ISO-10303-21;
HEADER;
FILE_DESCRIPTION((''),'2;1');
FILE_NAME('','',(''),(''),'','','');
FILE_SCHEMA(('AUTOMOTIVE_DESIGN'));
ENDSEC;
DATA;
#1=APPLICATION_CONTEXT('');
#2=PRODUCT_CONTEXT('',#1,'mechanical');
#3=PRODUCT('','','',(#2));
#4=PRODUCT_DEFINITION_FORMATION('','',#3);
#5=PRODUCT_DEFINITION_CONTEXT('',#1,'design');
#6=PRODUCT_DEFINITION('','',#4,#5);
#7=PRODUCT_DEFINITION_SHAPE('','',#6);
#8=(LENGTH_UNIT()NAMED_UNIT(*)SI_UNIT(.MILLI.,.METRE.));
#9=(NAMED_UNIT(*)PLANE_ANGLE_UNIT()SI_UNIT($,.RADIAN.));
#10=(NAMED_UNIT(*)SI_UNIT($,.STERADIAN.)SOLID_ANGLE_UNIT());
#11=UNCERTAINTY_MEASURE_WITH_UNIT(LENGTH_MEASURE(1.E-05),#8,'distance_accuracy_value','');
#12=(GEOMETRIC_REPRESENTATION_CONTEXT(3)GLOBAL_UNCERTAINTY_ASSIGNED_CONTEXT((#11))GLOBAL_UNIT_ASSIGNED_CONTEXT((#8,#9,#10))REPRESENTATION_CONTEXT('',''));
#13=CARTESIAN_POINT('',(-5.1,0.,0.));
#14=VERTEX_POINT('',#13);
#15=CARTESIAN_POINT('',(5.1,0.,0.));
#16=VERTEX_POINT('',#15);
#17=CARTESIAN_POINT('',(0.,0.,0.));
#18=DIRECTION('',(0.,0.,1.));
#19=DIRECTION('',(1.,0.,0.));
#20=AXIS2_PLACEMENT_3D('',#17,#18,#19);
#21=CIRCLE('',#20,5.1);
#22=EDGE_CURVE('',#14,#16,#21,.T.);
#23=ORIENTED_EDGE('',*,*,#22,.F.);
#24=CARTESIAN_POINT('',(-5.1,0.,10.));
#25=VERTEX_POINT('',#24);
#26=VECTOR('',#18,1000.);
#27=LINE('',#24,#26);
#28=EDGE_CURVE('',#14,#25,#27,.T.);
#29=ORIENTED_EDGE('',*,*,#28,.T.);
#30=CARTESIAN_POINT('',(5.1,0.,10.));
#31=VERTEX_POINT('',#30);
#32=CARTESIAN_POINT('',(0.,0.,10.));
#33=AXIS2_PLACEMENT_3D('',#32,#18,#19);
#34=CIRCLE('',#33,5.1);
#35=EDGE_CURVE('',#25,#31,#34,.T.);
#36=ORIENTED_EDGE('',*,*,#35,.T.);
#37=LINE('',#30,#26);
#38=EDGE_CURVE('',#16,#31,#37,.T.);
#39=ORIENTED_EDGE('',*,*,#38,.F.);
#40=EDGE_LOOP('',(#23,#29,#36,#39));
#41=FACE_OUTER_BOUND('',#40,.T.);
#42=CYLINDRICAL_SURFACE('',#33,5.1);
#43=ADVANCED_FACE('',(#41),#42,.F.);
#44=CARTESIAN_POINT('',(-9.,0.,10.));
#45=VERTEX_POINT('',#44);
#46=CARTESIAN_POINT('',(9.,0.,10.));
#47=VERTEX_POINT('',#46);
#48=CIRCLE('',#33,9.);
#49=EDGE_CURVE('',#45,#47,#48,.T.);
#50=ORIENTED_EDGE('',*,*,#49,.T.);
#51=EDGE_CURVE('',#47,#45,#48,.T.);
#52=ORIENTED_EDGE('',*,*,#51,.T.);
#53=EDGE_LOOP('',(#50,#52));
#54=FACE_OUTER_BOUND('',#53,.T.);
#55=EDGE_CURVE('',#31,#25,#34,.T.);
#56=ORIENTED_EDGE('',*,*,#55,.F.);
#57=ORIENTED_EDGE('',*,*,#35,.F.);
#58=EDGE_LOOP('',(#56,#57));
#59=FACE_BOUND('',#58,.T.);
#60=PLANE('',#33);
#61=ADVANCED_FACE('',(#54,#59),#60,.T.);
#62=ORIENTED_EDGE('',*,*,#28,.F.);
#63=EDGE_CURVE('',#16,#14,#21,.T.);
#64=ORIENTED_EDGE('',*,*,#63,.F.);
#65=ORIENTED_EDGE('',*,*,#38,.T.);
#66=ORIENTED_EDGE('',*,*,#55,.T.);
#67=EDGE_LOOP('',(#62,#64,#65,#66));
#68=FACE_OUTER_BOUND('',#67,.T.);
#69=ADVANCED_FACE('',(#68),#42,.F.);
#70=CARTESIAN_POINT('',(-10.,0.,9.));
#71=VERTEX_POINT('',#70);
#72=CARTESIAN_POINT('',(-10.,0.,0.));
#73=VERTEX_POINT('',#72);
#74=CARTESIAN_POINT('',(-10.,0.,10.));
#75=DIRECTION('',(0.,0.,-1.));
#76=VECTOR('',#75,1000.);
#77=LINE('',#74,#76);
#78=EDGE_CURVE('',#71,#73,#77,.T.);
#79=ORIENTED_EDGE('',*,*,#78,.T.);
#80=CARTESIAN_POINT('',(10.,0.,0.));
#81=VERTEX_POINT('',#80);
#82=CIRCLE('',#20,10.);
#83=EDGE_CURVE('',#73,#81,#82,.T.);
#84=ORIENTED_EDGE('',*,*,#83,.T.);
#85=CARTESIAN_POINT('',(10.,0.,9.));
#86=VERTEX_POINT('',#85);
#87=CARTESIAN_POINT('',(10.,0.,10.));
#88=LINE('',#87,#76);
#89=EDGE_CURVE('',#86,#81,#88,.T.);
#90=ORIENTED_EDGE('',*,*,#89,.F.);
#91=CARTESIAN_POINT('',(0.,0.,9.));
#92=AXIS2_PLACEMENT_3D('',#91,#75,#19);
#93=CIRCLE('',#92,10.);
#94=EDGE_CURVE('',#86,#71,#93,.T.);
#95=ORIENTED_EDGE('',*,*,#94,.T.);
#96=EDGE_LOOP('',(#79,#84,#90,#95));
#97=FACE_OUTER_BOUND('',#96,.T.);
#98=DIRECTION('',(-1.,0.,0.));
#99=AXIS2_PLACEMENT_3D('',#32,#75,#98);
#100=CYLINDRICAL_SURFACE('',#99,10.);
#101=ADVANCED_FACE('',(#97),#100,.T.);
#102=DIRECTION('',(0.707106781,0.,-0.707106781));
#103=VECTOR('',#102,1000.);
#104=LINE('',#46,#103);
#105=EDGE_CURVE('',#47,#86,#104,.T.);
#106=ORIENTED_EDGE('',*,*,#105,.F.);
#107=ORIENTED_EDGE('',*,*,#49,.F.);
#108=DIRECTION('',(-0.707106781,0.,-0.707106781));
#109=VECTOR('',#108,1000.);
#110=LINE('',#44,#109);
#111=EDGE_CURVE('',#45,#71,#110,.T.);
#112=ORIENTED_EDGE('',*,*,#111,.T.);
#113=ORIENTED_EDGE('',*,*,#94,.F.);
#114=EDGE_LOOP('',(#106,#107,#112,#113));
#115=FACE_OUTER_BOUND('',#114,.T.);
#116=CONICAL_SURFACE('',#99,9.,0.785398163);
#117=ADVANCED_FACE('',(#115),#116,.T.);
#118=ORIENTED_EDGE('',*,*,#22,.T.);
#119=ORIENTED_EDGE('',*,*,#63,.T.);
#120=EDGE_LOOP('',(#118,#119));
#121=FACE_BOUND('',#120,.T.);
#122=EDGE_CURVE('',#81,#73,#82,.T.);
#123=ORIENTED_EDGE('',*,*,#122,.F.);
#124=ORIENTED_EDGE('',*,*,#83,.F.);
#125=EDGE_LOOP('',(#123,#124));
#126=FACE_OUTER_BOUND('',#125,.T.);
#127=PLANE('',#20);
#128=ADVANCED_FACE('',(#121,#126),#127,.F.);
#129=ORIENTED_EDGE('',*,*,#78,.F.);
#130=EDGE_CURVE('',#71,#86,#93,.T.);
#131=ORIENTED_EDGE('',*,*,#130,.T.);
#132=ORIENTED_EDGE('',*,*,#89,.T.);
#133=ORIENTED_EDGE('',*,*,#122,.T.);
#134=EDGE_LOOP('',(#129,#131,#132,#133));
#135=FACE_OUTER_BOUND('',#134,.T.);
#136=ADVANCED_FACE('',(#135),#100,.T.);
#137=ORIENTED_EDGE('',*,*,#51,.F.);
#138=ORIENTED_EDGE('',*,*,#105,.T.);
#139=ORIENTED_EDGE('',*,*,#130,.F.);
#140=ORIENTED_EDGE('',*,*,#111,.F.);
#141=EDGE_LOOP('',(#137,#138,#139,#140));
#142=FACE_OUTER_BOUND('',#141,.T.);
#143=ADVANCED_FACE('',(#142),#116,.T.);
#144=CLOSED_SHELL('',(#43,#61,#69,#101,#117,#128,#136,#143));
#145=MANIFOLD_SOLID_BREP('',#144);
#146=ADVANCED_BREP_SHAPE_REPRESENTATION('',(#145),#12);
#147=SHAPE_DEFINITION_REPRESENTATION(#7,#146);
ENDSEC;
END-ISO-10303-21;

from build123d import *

# Parameters (mm, degrees)
SKETCH_1_R              = 10
EXTRUDE_1_DEPTH         = 10
HOLE_WIZARD_M12_1_D     = 10.2
HOLE_WIZARD_M12_1_DEPTH = 30.25
HOLE_WIZARD_M12_1_TIP   = 3.064389157
CHAMFER_1_SIZE          = 1


with BuildPart() as part:
    # 草图1 → 凸台-拉伸1 (new body)
    with BuildSketch(Plane.XY):
        Circle(SKETCH_1_R)
    extrude(amount=EXTRUDE_1_DEPTH)

    # M12 螺纹孔1
    with Locations(Plane.XY.offset(10)):
        with Locations((0, 0)):
            Hole(HOLE_WIZARD_M12_1_D / 2, depth=HOLE_WIZARD_M12_1_DEPTH)
            with Locations((0, 0, -(HOLE_WIZARD_M12_1_DEPTH + HOLE_WIZARD_M12_1_TIP / 2))):  # 118° drill point
                Cone(0, HOLE_WIZARD_M12_1_D / 2, HOLE_WIZARD_M12_1_TIP, mode=Mode.SUBTRACT)

    # 倒角1
    chamfer_1_edges = [part.edges().sort_by_distance(p)[0] for p in [
        (-10, 0, 10),
    ]]
    chamfer(chamfer_1_edges, length=CHAMFER_1_SIZE)


solid = part.part
